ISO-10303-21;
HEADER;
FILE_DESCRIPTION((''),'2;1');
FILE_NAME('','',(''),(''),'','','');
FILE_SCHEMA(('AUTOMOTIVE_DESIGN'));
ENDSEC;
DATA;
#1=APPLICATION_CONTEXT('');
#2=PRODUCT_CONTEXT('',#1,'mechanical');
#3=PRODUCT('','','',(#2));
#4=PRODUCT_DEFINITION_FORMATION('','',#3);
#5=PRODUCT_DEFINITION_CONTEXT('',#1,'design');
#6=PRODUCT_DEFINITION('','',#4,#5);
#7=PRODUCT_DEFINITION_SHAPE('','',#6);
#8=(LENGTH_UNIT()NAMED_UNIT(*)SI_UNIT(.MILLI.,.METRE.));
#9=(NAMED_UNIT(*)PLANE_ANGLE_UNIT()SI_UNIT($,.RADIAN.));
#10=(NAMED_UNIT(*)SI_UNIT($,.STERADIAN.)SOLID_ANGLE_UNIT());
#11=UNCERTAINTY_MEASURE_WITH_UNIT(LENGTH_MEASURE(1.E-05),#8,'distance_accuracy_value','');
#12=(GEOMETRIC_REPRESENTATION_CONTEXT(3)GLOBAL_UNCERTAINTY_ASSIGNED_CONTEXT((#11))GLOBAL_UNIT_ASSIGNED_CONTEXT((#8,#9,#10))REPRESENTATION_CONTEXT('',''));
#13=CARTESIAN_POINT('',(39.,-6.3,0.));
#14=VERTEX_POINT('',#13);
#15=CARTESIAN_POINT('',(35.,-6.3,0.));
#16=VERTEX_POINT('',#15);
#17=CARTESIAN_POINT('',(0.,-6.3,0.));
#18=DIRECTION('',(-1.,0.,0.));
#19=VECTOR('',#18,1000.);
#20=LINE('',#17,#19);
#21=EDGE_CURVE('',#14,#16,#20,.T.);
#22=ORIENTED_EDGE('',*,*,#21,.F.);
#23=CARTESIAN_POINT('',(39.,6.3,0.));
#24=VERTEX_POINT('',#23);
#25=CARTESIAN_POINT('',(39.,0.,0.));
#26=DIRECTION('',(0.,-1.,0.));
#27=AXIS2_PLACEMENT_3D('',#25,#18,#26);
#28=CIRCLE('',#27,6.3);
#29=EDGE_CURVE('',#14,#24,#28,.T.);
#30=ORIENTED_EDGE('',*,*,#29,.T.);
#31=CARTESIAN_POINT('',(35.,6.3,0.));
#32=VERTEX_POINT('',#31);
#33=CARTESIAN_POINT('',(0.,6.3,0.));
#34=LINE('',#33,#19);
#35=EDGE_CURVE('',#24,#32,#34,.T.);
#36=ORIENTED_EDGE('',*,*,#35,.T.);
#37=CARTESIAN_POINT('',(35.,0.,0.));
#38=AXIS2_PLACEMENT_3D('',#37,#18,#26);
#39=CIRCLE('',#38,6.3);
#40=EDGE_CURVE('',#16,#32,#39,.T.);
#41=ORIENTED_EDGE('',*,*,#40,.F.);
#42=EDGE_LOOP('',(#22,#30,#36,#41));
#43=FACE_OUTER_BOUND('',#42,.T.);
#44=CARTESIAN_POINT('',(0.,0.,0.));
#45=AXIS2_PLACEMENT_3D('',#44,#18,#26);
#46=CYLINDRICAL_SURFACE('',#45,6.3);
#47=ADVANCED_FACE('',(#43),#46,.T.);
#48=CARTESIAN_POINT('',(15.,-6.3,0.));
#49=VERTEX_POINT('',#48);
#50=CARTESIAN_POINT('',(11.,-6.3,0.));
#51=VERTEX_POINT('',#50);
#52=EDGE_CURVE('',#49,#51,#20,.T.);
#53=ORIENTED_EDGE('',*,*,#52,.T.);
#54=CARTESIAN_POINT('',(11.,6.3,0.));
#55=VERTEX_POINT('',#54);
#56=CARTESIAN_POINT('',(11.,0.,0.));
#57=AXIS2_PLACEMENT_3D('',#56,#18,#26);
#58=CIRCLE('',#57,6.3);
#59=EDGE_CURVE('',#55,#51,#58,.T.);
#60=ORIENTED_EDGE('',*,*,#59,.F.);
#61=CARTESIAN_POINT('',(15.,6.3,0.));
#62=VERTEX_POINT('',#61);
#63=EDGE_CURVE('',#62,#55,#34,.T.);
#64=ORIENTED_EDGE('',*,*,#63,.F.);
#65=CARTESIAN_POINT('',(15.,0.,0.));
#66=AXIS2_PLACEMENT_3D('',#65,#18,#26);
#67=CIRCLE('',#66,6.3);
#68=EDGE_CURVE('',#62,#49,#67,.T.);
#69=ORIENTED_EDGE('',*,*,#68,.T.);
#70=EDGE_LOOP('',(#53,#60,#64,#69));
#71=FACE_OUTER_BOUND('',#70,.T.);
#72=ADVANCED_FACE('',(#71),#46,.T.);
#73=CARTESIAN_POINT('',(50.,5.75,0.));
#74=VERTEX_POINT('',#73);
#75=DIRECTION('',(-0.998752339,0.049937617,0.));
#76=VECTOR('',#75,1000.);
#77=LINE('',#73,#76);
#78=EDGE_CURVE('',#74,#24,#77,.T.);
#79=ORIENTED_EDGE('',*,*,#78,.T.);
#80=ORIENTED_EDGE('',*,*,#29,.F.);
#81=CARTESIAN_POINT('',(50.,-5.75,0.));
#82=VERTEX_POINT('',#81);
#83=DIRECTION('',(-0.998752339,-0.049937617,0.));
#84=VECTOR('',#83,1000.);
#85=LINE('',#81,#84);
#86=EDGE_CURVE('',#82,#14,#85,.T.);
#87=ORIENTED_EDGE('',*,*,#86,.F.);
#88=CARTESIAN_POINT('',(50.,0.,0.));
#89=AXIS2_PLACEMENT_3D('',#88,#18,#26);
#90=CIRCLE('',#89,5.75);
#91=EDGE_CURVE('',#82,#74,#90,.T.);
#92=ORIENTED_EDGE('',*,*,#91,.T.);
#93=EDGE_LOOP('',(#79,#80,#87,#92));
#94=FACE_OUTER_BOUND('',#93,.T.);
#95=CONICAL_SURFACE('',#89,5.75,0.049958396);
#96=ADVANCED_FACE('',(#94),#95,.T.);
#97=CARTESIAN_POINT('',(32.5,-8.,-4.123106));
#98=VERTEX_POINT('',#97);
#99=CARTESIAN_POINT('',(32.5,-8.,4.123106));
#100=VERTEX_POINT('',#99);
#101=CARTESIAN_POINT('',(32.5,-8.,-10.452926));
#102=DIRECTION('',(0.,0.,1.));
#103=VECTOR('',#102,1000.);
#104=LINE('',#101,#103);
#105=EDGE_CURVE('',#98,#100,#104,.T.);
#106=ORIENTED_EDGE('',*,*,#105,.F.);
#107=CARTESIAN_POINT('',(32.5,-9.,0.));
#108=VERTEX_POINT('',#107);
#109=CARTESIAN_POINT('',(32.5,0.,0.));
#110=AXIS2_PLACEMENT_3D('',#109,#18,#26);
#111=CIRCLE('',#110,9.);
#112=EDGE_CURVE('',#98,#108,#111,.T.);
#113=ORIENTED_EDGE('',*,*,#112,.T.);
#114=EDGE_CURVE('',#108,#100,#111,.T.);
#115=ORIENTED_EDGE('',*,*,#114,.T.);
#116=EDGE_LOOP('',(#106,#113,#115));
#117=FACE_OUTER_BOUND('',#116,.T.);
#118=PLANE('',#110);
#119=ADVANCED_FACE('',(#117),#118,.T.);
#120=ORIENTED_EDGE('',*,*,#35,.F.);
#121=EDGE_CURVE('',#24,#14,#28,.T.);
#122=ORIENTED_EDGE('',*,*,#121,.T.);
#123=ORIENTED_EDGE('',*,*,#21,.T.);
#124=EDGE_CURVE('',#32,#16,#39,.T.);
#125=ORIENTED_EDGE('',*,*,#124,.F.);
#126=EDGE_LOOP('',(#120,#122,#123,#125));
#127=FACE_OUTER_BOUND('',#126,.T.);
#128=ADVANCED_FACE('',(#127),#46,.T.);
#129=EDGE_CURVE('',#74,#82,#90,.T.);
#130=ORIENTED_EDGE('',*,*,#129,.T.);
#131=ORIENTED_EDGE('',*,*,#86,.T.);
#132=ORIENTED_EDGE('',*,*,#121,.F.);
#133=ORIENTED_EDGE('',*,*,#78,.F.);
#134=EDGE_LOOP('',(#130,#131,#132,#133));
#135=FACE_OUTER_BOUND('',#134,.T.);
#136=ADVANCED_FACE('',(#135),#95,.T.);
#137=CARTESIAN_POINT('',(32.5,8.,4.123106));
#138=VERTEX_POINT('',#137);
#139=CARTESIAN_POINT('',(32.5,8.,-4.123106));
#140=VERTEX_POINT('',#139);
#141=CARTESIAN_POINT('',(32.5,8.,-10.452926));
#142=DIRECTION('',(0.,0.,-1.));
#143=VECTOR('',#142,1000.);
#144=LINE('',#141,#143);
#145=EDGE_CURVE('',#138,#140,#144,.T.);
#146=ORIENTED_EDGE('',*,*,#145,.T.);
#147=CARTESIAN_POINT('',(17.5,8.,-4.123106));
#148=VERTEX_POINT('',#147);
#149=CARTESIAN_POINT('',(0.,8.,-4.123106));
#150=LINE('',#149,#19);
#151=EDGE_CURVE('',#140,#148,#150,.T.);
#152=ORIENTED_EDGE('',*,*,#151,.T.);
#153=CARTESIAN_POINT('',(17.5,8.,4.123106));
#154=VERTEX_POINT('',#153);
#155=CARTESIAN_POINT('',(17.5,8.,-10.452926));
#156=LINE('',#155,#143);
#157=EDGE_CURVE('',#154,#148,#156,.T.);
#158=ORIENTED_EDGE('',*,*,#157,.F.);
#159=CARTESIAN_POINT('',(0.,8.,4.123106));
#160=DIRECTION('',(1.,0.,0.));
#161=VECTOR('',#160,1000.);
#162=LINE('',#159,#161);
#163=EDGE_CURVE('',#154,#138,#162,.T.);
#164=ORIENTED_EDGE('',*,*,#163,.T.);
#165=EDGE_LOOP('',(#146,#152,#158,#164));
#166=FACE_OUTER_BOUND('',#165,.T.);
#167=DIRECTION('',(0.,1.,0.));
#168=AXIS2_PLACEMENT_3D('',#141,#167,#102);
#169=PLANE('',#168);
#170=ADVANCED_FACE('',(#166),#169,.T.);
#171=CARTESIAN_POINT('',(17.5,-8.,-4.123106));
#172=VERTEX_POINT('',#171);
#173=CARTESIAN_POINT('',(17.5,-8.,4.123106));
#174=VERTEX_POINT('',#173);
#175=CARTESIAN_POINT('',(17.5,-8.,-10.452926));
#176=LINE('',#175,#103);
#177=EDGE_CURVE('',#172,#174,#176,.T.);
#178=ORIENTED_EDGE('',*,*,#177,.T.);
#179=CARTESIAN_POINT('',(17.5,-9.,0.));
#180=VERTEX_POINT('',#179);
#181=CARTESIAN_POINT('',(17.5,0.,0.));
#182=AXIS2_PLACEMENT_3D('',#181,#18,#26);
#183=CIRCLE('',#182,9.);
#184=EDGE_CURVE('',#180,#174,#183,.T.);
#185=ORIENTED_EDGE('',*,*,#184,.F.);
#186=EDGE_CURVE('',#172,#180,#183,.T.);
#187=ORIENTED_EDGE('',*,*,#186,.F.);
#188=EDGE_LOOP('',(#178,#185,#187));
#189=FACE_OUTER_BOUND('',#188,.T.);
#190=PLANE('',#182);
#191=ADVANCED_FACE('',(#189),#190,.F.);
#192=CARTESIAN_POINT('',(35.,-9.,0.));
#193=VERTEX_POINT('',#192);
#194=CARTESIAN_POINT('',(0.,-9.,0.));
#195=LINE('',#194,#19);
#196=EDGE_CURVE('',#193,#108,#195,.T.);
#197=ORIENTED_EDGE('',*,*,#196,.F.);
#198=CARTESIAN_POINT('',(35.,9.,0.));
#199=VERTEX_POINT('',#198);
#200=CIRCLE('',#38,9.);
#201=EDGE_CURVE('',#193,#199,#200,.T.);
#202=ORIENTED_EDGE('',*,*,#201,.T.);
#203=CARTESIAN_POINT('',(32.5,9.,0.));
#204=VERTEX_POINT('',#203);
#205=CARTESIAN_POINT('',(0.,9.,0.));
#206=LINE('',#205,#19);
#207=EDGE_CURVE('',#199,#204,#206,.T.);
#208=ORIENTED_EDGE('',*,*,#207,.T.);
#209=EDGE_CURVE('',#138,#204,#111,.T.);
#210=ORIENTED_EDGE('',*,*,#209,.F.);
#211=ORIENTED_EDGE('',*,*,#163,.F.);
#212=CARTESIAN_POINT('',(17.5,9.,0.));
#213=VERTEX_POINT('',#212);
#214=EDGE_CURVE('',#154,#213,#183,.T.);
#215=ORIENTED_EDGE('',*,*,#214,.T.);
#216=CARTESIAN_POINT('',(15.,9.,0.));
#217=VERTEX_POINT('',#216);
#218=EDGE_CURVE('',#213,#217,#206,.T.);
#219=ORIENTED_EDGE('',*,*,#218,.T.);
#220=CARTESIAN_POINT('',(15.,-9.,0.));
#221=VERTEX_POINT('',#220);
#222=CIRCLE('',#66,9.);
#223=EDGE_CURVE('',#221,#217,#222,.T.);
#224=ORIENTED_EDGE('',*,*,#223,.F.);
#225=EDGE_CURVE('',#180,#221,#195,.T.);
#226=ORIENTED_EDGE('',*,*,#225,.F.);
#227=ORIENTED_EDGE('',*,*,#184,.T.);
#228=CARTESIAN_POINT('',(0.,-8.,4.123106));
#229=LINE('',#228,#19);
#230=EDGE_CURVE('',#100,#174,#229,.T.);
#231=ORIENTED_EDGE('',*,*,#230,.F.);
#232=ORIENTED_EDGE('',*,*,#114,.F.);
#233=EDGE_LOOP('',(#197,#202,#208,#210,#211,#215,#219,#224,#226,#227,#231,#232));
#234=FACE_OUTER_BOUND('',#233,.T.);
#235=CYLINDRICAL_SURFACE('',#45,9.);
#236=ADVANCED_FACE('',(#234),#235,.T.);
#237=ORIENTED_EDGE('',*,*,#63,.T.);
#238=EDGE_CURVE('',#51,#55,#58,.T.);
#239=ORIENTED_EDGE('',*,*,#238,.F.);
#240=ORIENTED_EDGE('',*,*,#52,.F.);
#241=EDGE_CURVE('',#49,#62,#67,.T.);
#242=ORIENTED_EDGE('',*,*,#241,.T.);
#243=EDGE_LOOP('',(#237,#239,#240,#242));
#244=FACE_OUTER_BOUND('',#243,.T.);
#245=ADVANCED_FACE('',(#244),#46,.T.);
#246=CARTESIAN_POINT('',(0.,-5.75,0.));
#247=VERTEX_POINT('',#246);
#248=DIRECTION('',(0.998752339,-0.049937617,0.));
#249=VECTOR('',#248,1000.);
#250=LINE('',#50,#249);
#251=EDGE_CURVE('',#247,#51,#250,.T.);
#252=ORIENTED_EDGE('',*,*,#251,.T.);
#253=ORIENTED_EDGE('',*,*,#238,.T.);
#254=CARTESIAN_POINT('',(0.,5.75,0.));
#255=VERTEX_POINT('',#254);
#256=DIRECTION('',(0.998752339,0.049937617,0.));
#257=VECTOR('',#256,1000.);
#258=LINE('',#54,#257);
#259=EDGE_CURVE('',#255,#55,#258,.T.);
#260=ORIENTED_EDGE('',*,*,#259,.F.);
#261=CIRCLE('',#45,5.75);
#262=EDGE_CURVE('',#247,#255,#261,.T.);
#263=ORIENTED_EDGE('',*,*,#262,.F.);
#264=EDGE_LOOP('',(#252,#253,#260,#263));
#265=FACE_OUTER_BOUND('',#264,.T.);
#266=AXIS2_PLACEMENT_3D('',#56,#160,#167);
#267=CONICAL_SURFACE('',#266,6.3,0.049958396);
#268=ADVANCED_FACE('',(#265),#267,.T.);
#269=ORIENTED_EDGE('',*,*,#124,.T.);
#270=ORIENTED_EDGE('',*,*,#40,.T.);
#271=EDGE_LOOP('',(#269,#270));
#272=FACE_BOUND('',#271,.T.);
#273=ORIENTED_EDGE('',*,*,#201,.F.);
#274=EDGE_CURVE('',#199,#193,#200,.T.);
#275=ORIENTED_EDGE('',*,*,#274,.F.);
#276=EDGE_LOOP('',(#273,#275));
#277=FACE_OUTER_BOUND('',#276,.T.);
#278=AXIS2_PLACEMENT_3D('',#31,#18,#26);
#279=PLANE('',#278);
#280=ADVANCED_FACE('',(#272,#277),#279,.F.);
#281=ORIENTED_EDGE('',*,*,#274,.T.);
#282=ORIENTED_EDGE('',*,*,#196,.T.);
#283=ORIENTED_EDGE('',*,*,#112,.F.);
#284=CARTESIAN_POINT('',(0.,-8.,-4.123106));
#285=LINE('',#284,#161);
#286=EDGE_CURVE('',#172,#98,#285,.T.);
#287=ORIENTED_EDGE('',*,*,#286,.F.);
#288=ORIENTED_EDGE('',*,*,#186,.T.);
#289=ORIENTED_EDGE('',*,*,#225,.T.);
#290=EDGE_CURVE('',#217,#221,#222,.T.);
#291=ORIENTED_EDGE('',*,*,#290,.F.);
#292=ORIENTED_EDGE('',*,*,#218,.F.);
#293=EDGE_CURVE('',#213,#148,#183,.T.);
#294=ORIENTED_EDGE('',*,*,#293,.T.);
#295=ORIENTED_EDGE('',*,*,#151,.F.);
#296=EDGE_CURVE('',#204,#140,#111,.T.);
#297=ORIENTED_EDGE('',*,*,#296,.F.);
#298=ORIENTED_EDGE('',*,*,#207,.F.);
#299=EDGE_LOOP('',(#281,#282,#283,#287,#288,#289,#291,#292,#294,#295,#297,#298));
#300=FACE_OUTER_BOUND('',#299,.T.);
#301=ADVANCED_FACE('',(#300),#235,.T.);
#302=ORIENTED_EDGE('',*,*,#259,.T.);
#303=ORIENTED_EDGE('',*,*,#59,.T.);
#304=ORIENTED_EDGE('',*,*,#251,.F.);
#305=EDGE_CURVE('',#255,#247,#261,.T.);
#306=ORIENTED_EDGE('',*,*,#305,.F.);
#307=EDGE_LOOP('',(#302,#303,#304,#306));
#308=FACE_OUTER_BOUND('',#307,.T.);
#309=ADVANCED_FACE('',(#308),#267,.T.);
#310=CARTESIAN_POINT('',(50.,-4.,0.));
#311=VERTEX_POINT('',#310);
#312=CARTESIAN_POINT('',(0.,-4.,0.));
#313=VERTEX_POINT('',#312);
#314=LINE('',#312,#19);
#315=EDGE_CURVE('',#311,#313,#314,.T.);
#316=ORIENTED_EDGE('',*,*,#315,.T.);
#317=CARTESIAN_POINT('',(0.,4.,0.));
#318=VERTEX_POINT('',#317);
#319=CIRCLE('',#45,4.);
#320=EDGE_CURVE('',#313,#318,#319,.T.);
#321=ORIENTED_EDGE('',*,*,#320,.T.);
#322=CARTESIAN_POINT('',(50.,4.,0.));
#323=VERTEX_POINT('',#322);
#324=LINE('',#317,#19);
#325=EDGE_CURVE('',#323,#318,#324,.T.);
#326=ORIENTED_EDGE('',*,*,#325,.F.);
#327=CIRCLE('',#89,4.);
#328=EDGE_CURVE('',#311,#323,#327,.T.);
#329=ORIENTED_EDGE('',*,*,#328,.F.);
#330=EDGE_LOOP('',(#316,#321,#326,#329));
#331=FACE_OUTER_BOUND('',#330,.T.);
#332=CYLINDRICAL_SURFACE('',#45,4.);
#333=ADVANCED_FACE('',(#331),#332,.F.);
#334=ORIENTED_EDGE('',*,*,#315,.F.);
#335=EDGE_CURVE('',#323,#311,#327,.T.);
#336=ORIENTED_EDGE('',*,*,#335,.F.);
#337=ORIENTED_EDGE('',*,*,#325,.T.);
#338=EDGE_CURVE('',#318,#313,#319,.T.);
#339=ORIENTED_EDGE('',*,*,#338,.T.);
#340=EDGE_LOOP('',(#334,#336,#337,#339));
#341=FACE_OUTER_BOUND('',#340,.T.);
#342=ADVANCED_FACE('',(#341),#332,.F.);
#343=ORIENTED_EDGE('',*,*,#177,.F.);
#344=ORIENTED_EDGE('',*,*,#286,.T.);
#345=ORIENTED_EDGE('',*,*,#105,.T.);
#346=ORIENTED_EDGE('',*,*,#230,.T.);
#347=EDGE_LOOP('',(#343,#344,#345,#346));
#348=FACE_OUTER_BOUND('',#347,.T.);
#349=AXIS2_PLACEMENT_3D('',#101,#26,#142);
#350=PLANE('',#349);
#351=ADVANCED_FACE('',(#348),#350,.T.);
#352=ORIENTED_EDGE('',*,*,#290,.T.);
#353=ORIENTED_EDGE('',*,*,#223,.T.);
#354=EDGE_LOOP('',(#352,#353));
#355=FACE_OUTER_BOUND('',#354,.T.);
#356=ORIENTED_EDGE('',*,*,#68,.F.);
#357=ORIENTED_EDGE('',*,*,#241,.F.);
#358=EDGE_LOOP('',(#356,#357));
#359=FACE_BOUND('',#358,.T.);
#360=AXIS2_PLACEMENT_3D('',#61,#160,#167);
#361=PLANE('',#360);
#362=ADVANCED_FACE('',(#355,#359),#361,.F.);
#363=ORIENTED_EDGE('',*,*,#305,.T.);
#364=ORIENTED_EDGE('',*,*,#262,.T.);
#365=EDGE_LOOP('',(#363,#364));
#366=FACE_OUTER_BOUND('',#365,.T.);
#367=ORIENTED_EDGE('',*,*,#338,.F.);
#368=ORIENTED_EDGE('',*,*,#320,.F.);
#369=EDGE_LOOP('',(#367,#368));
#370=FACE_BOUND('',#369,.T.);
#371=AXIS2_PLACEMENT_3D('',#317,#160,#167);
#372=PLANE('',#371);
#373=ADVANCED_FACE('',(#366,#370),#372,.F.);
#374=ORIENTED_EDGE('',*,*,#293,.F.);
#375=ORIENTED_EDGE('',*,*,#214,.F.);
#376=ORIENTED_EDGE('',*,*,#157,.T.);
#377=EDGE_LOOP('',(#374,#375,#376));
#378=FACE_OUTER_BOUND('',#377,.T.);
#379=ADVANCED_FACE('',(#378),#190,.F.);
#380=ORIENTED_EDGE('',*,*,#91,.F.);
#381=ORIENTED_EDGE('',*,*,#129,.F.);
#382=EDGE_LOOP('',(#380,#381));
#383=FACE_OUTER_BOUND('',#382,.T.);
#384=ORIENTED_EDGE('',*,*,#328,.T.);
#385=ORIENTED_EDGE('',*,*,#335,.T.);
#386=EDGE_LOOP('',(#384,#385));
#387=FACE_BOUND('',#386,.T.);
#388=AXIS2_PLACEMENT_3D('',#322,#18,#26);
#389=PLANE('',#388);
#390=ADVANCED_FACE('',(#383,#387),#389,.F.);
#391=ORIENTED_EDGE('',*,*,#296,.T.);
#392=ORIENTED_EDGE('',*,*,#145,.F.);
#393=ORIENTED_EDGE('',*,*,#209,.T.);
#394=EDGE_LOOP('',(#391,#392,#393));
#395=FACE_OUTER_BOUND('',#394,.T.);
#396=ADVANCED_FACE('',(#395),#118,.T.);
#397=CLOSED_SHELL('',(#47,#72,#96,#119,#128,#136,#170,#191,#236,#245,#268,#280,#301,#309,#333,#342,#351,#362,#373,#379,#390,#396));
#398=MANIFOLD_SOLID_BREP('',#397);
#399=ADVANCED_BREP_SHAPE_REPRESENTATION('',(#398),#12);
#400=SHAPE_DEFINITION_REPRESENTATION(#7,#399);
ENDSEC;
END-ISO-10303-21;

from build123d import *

# Parameters (mm, degrees)
SKETCH_2_OUTSIDE_W   = 31.222
SKETCH_2_OUTSIDE_H   = 31.222
SKETCH_2_OUTSIDE_W_2 = 20.905852418
SKETCH_2_OUTSIDE_H_2 = 16
CUT_EXTRUDE_1_DEPTH  = 7.5


with BuildPart() as part:
    # 草图1 → 旋转1 (revolve)
    with BuildSketch(Plane.XY, mode=Mode.PRIVATE) as revolve_1_sk:
        Polygon((0, 4), (0, 5.75), (11, 6.3), (15, 6.3), (15, 9), (35, 9), (35, 6.3), (39, 6.3), (50, 5.75), (50, 4), align=None)
    revolve(revolve_1_sk.sketch.rotate(Axis((0, 0, 0), (1, 0, 0)), 180), axis=Axis((0, 0, 0), (1, 0, 0)))

    # 草图2 outside → 切除-拉伸1 (cut, symmetric)
    with BuildSketch(Plane.ZY.offset(-25)):
        Rectangle(SKETCH_2_OUTSIDE_W, SKETCH_2_OUTSIDE_H)
        Rectangle(SKETCH_2_OUTSIDE_W_2, SKETCH_2_OUTSIDE_H_2, mode=Mode.SUBTRACT)
    extrude(amount=CUT_EXTRUDE_1_DEPTH, both=True, mode=Mode.SUBTRACT)


solid = part.part
